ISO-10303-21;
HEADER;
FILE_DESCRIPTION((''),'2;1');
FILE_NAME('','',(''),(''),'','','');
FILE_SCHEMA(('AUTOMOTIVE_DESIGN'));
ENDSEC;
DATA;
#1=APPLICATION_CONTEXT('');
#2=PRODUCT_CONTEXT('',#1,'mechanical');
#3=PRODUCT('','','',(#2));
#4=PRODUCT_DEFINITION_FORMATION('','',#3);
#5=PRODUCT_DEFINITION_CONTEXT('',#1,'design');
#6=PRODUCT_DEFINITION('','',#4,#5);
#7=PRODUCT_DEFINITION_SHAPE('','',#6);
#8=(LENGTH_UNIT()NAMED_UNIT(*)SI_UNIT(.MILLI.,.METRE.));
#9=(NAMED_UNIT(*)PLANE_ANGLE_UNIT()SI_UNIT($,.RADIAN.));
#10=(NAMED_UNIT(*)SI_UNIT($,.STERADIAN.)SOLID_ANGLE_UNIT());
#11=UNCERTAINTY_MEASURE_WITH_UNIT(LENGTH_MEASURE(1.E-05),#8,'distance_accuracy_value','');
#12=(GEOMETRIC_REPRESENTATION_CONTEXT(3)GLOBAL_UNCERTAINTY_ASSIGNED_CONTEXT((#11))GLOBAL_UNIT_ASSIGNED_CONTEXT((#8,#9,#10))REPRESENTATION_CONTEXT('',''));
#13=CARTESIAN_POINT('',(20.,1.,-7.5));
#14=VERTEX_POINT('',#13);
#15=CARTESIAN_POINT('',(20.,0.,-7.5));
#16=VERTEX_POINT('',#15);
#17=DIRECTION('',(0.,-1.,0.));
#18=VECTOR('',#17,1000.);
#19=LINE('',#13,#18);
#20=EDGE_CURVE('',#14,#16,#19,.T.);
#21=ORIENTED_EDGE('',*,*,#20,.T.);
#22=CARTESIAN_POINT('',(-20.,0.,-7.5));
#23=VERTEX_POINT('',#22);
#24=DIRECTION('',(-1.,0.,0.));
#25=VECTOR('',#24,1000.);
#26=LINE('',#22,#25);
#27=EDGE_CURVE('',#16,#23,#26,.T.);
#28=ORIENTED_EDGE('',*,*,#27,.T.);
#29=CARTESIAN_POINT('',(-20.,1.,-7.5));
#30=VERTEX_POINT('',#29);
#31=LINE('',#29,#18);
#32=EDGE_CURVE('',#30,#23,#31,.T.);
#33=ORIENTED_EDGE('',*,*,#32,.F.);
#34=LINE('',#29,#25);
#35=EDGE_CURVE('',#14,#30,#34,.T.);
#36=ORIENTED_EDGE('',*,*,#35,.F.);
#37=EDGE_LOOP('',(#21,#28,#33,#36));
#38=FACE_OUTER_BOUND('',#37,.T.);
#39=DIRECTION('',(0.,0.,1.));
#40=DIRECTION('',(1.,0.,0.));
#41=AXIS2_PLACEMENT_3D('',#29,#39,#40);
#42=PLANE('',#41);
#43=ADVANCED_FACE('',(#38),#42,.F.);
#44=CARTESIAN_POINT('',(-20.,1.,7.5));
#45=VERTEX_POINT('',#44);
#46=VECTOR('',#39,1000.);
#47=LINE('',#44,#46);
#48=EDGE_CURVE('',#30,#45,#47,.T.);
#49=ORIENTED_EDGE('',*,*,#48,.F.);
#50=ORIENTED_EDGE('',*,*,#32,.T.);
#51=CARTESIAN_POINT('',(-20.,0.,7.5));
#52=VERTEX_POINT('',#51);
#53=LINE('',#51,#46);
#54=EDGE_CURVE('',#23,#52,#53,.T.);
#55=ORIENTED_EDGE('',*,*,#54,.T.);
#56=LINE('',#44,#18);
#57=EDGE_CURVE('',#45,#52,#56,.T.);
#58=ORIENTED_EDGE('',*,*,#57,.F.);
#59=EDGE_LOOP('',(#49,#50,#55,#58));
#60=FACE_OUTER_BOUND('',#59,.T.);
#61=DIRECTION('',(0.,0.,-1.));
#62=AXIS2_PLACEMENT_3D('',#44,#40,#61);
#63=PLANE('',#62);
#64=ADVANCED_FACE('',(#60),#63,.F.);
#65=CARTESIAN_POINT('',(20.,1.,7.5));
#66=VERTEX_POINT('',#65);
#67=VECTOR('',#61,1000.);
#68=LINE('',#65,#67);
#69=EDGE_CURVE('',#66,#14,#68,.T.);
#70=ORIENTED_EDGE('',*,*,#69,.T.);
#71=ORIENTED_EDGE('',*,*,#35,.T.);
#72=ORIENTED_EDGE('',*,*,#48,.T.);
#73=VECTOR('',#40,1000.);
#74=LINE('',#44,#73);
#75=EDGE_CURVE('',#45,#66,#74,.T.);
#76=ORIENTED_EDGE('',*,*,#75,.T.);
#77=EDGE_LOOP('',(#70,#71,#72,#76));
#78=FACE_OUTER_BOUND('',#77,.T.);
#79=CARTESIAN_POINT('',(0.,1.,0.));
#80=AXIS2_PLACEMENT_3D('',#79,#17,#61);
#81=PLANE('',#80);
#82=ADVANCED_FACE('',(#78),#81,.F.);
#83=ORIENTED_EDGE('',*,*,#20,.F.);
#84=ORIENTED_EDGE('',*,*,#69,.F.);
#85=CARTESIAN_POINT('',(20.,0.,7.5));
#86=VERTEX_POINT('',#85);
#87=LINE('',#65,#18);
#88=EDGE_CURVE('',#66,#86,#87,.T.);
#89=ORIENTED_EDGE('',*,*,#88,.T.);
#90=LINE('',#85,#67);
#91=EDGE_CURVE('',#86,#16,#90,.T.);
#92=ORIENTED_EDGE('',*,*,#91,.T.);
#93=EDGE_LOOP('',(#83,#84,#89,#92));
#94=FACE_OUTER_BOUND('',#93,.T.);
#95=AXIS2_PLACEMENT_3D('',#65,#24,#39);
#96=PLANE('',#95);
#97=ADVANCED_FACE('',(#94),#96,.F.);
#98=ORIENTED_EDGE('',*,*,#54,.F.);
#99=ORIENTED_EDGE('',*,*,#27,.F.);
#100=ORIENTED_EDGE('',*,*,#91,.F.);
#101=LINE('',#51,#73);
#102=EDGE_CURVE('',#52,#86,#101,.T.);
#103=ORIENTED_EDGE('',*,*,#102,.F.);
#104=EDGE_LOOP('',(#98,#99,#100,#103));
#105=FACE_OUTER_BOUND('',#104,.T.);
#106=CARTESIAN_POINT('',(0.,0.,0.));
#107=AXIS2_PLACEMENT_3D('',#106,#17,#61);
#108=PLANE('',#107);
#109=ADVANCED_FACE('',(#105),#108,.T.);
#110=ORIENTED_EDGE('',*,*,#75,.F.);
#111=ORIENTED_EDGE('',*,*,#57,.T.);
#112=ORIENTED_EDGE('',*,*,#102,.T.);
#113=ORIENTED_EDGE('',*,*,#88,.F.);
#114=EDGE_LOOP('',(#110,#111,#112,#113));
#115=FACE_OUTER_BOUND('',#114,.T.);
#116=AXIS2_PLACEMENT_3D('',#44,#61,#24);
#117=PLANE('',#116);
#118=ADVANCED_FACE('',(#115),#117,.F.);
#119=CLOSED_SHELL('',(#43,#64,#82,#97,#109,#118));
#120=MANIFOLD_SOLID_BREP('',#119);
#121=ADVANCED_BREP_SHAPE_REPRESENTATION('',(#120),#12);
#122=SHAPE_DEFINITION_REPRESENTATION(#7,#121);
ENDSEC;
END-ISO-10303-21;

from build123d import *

# Parameters (mm, degrees)
SKETCH_1_W      = 40
SKETCH_1_H      = 15
EXTRUDE_1_DEPTH = 1


with BuildPart() as part:
    # 草图1 → 凸台-拉伸1 (new body)
    with BuildSketch(Plane(origin=(0, 0, 0), x_dir=(1, 0, 0), z_dir=(0, 1, 0))):
        Rectangle(SKETCH_1_W, SKETCH_1_H)
    extrude(amount=EXTRUDE_1_DEPTH)


solid = part.part
